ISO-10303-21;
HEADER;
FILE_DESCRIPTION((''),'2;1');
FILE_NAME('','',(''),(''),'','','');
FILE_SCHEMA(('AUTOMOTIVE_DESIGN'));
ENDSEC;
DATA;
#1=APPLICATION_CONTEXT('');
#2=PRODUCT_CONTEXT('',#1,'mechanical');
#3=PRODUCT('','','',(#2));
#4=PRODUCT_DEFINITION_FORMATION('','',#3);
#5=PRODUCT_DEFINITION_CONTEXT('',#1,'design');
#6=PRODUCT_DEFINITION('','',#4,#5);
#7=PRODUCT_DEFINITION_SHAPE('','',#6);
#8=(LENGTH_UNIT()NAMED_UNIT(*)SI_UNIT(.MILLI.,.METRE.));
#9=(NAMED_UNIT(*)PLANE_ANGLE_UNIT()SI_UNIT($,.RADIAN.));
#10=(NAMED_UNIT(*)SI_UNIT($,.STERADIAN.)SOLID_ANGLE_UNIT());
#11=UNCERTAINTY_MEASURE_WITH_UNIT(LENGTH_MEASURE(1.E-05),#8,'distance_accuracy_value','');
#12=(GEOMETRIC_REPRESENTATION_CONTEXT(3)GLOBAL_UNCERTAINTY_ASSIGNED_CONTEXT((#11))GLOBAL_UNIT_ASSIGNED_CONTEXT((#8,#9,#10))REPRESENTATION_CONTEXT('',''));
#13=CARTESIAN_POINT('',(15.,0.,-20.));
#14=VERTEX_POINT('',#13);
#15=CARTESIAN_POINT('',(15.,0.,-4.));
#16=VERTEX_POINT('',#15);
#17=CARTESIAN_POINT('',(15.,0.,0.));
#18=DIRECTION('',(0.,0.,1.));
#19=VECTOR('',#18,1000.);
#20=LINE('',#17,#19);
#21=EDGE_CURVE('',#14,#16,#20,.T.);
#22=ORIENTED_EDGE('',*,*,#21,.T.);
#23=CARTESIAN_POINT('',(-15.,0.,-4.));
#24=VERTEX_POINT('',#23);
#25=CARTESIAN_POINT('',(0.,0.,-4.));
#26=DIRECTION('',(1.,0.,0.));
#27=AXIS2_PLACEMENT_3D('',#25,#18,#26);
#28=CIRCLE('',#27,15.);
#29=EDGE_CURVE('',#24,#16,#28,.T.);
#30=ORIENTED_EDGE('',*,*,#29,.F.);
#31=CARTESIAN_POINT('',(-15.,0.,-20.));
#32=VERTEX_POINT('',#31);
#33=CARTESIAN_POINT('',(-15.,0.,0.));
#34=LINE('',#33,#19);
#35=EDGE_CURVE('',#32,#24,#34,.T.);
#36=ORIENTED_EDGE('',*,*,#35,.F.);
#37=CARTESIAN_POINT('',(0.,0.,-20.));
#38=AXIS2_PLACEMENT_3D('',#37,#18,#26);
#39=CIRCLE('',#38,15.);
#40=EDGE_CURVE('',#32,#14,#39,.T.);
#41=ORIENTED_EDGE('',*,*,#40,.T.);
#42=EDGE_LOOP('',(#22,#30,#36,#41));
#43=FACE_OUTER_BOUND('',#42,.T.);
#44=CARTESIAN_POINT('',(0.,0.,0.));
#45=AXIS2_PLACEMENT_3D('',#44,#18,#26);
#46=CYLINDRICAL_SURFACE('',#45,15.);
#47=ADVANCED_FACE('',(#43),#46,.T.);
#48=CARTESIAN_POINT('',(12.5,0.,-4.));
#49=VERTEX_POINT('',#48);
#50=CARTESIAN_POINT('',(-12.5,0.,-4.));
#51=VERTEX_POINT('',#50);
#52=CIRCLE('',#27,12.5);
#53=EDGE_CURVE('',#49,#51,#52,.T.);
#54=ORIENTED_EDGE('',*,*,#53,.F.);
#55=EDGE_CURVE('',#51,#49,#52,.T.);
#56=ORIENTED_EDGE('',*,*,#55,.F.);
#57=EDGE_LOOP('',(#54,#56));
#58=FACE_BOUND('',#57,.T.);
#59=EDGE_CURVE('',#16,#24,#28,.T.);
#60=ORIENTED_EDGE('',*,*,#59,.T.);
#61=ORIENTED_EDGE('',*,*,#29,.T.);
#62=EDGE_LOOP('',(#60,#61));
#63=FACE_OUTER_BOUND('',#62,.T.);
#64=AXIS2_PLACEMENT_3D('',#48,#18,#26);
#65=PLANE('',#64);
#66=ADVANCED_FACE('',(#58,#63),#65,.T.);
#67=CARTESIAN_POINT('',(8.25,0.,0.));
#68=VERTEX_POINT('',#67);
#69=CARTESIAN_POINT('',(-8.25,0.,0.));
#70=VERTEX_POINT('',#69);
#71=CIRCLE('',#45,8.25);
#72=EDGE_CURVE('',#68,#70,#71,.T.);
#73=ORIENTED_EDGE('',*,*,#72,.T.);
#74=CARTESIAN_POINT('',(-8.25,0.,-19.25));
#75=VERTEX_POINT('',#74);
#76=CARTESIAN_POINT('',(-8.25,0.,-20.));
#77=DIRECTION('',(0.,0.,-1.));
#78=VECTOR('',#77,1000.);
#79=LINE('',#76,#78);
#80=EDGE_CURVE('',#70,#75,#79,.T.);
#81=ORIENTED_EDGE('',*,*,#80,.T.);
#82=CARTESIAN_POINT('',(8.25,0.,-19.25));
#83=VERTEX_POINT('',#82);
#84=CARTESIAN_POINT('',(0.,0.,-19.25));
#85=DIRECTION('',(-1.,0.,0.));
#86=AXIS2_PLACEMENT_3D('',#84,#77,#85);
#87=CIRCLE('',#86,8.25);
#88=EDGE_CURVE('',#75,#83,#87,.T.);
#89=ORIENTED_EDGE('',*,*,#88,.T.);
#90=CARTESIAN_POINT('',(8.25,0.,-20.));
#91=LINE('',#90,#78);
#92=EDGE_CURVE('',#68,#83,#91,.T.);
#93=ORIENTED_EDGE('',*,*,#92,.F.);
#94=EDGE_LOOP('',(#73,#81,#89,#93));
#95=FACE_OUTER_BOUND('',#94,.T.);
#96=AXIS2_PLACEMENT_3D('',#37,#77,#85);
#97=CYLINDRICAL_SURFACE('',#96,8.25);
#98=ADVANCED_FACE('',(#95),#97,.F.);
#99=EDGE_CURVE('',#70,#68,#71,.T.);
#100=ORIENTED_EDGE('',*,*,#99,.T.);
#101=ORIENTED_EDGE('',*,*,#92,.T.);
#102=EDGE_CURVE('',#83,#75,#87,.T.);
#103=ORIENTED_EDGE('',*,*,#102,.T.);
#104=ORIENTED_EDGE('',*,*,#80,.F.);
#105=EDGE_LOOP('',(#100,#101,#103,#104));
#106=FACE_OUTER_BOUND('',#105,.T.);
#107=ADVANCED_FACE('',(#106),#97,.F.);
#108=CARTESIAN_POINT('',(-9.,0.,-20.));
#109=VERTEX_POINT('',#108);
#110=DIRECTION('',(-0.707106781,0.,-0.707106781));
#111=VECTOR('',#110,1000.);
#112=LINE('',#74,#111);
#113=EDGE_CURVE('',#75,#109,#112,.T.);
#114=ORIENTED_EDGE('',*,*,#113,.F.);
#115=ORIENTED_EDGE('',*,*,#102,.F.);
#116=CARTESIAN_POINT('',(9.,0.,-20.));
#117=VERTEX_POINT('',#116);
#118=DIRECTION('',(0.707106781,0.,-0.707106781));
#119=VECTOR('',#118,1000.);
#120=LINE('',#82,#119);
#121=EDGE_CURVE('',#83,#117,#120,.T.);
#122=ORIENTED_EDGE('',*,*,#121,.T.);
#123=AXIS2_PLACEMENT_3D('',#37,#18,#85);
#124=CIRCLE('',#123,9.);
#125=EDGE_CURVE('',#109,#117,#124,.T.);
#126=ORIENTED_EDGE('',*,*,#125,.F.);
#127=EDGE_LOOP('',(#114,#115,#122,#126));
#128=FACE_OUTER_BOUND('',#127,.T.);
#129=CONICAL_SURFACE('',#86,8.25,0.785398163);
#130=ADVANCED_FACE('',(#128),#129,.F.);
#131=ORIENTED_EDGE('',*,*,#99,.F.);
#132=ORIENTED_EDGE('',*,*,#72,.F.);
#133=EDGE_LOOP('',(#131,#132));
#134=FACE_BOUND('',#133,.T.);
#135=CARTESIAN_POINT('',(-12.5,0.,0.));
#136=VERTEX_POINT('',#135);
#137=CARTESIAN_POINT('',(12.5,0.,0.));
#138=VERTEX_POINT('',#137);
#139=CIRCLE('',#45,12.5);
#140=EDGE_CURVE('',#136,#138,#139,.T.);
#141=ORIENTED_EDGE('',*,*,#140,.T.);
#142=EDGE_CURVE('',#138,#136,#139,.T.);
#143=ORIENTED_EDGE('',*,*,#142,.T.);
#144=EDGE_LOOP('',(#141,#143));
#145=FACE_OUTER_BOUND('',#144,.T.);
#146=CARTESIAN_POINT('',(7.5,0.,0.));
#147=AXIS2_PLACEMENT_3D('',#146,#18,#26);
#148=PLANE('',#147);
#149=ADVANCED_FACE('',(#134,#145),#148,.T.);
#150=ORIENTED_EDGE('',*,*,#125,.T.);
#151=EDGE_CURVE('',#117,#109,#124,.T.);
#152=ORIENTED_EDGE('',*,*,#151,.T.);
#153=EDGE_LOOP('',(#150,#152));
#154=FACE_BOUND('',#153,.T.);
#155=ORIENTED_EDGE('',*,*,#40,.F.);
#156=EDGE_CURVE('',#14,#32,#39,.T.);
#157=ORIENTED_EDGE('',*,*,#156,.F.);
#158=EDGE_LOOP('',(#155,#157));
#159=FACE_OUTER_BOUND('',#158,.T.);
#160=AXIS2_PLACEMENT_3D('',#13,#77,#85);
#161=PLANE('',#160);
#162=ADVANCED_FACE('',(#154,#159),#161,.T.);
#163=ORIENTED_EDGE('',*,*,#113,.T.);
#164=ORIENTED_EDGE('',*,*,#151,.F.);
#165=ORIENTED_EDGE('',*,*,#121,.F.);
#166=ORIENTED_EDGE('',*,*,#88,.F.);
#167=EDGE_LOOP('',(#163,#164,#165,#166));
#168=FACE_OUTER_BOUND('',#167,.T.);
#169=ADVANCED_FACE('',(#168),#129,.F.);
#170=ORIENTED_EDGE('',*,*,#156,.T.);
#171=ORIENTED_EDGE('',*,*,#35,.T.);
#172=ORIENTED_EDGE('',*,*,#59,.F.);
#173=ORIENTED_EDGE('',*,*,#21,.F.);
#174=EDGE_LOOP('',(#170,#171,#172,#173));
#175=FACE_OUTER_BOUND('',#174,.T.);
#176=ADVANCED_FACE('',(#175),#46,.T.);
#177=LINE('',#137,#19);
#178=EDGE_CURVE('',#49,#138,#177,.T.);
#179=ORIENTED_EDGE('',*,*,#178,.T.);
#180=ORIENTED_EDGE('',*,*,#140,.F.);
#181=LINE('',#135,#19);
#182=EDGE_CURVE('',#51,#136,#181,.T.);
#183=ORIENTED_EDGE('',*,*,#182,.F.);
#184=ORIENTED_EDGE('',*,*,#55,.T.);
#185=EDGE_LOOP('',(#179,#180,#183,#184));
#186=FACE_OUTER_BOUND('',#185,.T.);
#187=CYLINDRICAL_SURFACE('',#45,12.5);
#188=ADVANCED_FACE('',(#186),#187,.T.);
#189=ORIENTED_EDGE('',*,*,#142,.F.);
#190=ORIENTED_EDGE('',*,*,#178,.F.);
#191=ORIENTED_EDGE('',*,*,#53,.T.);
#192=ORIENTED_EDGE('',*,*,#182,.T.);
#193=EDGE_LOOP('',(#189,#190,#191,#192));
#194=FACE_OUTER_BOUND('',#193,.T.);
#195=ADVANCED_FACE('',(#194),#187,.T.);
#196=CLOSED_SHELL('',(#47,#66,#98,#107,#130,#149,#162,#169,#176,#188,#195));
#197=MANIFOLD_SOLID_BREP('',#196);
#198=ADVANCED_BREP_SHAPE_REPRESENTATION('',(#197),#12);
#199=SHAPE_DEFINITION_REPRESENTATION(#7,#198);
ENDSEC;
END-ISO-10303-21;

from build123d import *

# Parameters (mm, degrees)
M18X1_5_TAPPED_HOLE1_D     = 16.5
M18X1_5_TAPPED_HOLE1_DEPTH = 43.5
M18X1_5_TAPPED_HOLE1_TIP   = 4.957100107
CHAMFER1_SIZE              = 0.75


with BuildPart() as part:
    # Sketch1 → Revolve1 (revolve)
    with BuildSketch(Plane(origin=(0, 0, 0), x_dir=(1, 0, 0), z_dir=(0, 1, 0))):
        Polygon((7.5, 0), (12.5, 0), (12.5, 4), (15, 4), (15, 20), (7.5, 20), align=None)
    revolve(axis=Axis((0, 0, 0), (0, 0, -1)))

    # M18x1.5 Tapped Hole1
    with Locations(Plane(origin=(0, 0, -20), x_dir=(-1, 0, 0), z_dir=(0, 0, -1))):
        with Locations((0, 0)):
            Hole(M18X1_5_TAPPED_HOLE1_D / 2, depth=M18X1_5_TAPPED_HOLE1_DEPTH)
            with Locations((0, 0, -(M18X1_5_TAPPED_HOLE1_DEPTH + M18X1_5_TAPPED_HOLE1_TIP / 2))):  # 118° drill point
                Cone(0, M18X1_5_TAPPED_HOLE1_D / 2, M18X1_5_TAPPED_HOLE1_TIP, mode=Mode.SUBTRACT)

    # Chamfer1
    chamfer1_edges = [part.edges().sort_by_distance(p)[0] for p in [
        (-8.25, 0, -20),
    ]]
    chamfer(chamfer1_edges, length=CHAMFER1_SIZE)


solid = part.part
